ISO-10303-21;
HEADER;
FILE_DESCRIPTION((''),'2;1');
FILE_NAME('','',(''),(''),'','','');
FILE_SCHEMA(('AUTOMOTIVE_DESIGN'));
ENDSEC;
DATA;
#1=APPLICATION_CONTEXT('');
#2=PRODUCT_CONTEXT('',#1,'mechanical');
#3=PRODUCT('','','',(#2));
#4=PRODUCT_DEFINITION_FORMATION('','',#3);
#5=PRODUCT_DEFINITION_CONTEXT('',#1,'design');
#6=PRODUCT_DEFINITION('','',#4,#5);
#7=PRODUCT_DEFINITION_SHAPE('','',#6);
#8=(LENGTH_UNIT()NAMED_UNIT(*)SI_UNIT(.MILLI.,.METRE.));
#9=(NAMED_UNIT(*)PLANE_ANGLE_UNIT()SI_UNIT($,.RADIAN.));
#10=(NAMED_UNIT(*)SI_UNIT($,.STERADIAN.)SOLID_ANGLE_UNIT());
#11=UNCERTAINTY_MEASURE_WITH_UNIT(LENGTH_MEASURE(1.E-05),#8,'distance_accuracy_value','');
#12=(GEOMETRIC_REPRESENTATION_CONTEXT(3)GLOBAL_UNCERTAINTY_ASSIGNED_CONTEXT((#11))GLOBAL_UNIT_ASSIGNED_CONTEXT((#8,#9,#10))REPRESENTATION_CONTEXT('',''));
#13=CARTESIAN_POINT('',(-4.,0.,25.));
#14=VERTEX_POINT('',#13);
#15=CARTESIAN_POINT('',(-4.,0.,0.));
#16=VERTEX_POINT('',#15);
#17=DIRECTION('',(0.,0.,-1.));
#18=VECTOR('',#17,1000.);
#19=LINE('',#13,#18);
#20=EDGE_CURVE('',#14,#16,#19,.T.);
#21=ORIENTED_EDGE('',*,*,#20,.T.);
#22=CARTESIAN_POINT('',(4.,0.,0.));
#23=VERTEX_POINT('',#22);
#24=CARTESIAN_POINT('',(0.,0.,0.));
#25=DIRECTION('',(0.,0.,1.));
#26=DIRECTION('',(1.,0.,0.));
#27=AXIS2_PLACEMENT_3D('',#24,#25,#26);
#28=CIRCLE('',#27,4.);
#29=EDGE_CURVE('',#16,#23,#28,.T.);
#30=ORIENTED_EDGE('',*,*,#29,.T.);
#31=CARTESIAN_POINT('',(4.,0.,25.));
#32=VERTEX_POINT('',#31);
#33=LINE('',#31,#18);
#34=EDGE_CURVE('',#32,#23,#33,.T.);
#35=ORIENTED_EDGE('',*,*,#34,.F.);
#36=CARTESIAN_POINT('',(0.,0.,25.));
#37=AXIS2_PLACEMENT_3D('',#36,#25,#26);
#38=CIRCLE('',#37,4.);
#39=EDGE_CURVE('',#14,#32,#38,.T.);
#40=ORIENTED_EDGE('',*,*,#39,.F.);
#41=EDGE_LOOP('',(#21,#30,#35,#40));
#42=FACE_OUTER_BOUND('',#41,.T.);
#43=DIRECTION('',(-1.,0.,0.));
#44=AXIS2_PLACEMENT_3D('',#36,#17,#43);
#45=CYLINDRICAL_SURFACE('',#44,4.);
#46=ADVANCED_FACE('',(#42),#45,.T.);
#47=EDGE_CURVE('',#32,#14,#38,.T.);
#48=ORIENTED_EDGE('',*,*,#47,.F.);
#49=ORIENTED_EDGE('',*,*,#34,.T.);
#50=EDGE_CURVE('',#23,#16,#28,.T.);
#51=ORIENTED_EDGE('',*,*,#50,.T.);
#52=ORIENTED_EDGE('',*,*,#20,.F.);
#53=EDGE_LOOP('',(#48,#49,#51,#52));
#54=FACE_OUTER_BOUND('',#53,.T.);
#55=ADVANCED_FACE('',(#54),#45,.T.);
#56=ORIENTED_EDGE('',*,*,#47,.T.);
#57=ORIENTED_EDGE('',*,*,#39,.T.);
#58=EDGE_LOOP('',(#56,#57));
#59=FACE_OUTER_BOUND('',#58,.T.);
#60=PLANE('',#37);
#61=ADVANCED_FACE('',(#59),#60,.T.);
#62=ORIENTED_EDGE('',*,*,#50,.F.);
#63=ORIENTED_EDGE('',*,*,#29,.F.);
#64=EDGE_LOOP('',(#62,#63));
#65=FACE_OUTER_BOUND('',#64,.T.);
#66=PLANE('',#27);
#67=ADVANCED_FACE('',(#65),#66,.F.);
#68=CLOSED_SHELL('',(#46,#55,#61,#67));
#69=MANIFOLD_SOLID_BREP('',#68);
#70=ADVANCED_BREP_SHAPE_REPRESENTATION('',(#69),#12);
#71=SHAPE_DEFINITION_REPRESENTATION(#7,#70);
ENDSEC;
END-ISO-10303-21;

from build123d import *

# Parameters (mm, degrees)
SKETCH1_R           = 4
BOSS_EXTRUDE1_DEPTH = 25


with BuildPart() as part:
    # Sketch1 → Boss-Extrude1 (new body)
    with BuildSketch(Plane.XY):
        Circle(SKETCH1_R)
    extrude(amount=BOSS_EXTRUDE1_DEPTH)


solid = part.part
